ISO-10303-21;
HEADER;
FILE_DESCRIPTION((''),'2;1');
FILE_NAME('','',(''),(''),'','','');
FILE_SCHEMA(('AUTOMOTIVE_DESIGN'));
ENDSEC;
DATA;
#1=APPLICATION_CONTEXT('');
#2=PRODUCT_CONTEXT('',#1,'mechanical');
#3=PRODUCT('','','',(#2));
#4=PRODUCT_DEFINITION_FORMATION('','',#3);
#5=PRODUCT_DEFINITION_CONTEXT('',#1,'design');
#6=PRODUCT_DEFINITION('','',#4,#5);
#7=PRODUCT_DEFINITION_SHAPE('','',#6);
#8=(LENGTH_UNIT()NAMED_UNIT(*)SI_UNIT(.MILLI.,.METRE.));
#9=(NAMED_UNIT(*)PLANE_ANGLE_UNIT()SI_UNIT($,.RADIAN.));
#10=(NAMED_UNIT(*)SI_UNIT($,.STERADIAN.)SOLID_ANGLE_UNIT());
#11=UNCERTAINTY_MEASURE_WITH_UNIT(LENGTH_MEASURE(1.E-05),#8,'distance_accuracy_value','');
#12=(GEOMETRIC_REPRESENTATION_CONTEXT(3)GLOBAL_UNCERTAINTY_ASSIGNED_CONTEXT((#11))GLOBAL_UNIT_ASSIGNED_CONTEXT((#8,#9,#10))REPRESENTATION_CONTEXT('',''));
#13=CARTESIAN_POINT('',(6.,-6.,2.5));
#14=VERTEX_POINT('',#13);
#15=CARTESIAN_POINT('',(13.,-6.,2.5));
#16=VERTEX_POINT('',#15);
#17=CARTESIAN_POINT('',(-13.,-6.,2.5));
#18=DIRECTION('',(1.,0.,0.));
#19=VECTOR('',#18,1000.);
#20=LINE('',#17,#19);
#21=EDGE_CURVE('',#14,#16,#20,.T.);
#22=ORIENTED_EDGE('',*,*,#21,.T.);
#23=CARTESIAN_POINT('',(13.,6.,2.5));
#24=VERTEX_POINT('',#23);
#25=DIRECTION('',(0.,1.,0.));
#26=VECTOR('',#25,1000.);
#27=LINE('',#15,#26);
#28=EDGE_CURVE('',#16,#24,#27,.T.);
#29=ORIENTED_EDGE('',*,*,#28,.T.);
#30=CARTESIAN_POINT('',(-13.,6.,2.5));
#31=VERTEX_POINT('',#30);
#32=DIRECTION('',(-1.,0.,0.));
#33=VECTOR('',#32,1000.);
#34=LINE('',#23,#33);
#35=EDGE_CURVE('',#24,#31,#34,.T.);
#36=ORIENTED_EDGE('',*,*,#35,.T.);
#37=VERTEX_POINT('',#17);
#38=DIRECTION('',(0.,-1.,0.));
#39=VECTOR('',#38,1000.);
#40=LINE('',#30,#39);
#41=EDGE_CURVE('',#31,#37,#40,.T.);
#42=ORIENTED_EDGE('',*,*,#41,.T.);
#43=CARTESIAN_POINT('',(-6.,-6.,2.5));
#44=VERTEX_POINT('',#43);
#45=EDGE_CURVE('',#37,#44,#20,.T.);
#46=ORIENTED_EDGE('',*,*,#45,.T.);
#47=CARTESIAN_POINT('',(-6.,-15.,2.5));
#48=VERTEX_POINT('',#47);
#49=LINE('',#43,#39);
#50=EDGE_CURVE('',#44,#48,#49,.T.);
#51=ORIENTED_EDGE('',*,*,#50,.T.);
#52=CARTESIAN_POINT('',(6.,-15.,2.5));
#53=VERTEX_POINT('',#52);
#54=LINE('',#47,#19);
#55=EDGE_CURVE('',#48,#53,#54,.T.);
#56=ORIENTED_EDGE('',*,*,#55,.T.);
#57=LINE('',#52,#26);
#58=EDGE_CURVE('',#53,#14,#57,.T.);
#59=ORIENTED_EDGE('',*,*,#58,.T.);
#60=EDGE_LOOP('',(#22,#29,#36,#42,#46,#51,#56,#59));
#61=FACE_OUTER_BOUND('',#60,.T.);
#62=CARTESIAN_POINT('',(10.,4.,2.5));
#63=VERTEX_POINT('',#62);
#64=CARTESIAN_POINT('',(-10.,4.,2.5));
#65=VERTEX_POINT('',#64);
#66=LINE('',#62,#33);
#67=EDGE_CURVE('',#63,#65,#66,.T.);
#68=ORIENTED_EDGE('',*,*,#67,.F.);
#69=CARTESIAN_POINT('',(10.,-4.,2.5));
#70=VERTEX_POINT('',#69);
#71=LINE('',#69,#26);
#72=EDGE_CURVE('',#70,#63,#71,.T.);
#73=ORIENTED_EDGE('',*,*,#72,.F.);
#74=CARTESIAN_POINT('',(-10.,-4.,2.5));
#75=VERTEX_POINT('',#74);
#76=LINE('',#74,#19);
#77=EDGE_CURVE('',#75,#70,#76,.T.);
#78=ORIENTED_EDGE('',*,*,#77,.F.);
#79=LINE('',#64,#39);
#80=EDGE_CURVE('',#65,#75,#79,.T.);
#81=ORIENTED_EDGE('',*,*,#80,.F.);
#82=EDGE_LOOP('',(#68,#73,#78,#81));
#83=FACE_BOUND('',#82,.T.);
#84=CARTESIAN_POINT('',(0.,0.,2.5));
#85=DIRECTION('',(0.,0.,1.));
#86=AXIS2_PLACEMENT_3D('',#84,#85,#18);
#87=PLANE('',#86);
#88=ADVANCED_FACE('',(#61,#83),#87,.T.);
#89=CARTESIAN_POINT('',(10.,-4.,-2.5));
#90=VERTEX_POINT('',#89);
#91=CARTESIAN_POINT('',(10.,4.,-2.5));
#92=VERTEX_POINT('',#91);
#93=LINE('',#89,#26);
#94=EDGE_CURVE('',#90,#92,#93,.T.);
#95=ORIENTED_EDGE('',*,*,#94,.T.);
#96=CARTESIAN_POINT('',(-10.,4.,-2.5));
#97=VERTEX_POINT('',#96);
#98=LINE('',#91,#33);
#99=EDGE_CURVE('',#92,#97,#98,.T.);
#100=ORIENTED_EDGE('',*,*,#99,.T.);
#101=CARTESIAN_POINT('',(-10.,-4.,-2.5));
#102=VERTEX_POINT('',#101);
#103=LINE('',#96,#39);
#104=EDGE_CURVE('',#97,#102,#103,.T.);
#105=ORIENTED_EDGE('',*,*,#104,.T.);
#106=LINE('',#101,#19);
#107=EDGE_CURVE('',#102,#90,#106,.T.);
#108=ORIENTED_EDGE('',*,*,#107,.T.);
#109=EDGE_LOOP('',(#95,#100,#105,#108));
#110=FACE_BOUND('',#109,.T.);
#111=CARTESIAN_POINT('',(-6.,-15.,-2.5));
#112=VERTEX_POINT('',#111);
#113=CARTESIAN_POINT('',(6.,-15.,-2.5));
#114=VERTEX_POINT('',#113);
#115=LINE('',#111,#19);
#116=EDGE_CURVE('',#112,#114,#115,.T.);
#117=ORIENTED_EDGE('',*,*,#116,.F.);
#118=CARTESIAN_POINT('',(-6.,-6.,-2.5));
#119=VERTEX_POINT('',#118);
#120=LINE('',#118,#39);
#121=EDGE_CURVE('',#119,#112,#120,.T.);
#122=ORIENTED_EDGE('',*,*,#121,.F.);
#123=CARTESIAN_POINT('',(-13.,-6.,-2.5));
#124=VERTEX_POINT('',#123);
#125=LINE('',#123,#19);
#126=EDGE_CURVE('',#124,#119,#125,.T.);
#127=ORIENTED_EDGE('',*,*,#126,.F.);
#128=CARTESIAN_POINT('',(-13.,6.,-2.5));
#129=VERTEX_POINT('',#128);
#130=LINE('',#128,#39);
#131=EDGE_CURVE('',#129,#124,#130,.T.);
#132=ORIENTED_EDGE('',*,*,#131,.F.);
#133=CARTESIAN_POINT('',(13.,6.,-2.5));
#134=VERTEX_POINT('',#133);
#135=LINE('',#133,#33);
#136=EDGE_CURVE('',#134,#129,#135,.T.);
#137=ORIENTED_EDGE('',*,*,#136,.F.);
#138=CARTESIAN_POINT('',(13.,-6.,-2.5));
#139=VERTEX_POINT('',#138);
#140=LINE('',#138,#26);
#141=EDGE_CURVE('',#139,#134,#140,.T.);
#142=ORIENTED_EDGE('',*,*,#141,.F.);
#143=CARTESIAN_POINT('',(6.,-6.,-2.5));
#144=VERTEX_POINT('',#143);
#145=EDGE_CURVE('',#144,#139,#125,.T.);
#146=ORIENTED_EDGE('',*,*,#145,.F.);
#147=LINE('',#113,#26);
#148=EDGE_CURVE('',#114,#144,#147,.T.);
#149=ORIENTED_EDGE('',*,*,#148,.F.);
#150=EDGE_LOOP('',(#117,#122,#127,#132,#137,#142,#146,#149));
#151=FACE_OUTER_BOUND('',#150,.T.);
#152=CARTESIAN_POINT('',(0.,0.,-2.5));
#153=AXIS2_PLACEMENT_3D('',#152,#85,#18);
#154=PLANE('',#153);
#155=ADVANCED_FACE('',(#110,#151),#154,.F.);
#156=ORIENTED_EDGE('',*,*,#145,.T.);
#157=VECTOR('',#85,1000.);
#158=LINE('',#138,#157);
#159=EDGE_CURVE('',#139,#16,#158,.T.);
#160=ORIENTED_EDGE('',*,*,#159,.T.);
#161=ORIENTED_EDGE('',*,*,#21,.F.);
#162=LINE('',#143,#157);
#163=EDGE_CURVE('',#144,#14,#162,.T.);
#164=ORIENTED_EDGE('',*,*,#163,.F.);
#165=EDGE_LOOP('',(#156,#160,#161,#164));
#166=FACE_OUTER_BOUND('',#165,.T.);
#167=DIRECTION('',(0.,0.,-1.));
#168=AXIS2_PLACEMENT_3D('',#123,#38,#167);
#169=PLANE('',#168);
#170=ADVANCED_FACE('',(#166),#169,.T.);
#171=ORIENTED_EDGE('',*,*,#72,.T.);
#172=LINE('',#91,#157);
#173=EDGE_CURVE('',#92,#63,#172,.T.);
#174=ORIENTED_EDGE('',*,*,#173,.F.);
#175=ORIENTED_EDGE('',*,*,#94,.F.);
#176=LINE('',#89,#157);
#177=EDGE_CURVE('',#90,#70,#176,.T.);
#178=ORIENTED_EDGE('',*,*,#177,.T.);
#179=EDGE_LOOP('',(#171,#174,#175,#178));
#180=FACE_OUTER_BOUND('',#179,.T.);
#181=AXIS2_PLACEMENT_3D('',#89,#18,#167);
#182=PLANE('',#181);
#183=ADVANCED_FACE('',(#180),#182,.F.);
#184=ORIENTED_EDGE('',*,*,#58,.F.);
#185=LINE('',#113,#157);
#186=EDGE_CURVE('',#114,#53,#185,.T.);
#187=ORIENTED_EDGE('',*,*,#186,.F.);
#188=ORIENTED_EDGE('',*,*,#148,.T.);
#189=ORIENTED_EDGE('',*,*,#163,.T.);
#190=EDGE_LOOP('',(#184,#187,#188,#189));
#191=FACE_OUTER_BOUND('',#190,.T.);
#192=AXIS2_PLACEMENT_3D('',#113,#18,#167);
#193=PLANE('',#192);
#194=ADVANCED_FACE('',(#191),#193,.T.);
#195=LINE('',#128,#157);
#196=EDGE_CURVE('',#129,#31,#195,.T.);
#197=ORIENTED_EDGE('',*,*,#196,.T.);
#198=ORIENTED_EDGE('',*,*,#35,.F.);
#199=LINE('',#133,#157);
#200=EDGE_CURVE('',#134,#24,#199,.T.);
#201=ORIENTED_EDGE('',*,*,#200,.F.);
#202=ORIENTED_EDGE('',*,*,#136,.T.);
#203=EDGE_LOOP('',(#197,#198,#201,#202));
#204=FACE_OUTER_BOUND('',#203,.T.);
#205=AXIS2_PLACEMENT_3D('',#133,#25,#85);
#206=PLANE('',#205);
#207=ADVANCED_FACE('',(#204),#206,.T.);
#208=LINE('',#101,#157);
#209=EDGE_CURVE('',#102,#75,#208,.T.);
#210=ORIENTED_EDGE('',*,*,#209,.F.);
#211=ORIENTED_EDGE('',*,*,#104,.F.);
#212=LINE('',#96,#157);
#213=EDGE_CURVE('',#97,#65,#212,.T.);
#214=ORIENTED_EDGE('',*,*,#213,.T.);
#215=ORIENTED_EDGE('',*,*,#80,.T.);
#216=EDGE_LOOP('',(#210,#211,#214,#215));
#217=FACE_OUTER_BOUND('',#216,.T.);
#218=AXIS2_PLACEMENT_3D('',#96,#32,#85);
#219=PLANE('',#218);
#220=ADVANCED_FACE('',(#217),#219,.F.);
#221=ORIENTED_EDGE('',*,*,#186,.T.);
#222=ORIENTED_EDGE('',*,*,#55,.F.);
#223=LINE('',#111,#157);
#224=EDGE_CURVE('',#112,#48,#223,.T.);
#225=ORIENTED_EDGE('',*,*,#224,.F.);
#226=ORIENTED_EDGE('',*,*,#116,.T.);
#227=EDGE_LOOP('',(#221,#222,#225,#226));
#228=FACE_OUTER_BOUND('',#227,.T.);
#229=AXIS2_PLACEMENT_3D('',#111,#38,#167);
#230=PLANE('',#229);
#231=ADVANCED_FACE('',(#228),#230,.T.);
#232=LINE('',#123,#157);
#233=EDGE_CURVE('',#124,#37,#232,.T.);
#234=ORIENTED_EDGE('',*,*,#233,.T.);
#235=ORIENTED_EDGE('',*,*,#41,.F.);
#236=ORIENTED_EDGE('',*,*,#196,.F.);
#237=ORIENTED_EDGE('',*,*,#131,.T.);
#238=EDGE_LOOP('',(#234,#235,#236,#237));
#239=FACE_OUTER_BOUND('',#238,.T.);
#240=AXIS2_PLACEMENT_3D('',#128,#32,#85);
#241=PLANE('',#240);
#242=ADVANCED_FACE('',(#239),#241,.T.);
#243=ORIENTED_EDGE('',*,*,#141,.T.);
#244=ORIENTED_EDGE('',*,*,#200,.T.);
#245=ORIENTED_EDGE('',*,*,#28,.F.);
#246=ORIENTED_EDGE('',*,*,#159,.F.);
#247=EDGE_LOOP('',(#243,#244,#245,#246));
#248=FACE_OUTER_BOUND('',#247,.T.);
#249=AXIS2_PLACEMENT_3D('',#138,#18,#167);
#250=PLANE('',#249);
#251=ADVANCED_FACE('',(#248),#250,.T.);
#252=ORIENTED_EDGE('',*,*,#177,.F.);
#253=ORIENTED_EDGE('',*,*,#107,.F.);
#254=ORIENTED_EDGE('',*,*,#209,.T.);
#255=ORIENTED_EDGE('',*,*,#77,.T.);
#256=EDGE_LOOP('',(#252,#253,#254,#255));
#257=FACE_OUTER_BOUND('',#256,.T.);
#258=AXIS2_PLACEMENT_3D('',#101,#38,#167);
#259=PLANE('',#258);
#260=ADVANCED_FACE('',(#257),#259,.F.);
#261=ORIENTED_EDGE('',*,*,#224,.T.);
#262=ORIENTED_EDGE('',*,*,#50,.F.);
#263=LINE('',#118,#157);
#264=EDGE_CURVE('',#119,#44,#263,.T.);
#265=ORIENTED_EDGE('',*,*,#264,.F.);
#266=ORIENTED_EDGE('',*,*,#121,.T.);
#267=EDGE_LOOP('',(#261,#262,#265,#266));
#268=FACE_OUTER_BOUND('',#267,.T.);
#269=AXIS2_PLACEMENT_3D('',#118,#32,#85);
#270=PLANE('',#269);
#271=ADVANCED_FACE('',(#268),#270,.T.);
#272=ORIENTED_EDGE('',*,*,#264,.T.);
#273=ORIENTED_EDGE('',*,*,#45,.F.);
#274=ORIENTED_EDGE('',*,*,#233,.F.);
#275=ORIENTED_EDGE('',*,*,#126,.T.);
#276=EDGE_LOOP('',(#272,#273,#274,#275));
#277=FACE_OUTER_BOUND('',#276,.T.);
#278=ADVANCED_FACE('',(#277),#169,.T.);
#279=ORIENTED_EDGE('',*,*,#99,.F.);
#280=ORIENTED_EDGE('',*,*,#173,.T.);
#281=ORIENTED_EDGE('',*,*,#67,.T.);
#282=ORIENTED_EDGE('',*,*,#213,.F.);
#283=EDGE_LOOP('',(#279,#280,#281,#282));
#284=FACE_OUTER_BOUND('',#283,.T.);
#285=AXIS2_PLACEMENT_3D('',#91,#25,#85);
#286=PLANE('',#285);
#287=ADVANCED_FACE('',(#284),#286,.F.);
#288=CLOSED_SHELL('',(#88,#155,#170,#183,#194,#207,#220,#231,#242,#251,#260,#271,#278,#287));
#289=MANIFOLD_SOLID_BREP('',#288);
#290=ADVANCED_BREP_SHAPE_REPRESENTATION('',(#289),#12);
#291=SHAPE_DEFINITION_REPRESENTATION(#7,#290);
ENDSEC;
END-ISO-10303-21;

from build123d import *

# Parameters (mm, degrees)
SKETCH_1_W      = 26
SKETCH_1_H      = 12
SKETCH_1_W_2    = 20
SKETCH_1_H_2    = 8
EXTRUDE_1_DEPTH = 2.5
SKETCH_2_W      = 12
SKETCH_2_H      = 9
EXTRUDE_2_DEPTH = 2.5


with BuildPart() as part:
    # 草图1 → 凸台-拉伸1 (new, symmetric)
    with BuildSketch(Plane.XY):
        Rectangle(SKETCH_1_W, SKETCH_1_H)
        Rectangle(SKETCH_1_W_2, SKETCH_1_H_2, mode=Mode.SUBTRACT)
    extrude(amount=EXTRUDE_1_DEPTH, both=True)

    # 草图2 → 凸台-拉伸2 (add, symmetric)
    with BuildSketch(Plane.XY):
        with Locations((0, -10.5)):
            Rectangle(SKETCH_2_W, SKETCH_2_H)
    extrude(amount=EXTRUDE_2_DEPTH, both=True)


solid = part.part
